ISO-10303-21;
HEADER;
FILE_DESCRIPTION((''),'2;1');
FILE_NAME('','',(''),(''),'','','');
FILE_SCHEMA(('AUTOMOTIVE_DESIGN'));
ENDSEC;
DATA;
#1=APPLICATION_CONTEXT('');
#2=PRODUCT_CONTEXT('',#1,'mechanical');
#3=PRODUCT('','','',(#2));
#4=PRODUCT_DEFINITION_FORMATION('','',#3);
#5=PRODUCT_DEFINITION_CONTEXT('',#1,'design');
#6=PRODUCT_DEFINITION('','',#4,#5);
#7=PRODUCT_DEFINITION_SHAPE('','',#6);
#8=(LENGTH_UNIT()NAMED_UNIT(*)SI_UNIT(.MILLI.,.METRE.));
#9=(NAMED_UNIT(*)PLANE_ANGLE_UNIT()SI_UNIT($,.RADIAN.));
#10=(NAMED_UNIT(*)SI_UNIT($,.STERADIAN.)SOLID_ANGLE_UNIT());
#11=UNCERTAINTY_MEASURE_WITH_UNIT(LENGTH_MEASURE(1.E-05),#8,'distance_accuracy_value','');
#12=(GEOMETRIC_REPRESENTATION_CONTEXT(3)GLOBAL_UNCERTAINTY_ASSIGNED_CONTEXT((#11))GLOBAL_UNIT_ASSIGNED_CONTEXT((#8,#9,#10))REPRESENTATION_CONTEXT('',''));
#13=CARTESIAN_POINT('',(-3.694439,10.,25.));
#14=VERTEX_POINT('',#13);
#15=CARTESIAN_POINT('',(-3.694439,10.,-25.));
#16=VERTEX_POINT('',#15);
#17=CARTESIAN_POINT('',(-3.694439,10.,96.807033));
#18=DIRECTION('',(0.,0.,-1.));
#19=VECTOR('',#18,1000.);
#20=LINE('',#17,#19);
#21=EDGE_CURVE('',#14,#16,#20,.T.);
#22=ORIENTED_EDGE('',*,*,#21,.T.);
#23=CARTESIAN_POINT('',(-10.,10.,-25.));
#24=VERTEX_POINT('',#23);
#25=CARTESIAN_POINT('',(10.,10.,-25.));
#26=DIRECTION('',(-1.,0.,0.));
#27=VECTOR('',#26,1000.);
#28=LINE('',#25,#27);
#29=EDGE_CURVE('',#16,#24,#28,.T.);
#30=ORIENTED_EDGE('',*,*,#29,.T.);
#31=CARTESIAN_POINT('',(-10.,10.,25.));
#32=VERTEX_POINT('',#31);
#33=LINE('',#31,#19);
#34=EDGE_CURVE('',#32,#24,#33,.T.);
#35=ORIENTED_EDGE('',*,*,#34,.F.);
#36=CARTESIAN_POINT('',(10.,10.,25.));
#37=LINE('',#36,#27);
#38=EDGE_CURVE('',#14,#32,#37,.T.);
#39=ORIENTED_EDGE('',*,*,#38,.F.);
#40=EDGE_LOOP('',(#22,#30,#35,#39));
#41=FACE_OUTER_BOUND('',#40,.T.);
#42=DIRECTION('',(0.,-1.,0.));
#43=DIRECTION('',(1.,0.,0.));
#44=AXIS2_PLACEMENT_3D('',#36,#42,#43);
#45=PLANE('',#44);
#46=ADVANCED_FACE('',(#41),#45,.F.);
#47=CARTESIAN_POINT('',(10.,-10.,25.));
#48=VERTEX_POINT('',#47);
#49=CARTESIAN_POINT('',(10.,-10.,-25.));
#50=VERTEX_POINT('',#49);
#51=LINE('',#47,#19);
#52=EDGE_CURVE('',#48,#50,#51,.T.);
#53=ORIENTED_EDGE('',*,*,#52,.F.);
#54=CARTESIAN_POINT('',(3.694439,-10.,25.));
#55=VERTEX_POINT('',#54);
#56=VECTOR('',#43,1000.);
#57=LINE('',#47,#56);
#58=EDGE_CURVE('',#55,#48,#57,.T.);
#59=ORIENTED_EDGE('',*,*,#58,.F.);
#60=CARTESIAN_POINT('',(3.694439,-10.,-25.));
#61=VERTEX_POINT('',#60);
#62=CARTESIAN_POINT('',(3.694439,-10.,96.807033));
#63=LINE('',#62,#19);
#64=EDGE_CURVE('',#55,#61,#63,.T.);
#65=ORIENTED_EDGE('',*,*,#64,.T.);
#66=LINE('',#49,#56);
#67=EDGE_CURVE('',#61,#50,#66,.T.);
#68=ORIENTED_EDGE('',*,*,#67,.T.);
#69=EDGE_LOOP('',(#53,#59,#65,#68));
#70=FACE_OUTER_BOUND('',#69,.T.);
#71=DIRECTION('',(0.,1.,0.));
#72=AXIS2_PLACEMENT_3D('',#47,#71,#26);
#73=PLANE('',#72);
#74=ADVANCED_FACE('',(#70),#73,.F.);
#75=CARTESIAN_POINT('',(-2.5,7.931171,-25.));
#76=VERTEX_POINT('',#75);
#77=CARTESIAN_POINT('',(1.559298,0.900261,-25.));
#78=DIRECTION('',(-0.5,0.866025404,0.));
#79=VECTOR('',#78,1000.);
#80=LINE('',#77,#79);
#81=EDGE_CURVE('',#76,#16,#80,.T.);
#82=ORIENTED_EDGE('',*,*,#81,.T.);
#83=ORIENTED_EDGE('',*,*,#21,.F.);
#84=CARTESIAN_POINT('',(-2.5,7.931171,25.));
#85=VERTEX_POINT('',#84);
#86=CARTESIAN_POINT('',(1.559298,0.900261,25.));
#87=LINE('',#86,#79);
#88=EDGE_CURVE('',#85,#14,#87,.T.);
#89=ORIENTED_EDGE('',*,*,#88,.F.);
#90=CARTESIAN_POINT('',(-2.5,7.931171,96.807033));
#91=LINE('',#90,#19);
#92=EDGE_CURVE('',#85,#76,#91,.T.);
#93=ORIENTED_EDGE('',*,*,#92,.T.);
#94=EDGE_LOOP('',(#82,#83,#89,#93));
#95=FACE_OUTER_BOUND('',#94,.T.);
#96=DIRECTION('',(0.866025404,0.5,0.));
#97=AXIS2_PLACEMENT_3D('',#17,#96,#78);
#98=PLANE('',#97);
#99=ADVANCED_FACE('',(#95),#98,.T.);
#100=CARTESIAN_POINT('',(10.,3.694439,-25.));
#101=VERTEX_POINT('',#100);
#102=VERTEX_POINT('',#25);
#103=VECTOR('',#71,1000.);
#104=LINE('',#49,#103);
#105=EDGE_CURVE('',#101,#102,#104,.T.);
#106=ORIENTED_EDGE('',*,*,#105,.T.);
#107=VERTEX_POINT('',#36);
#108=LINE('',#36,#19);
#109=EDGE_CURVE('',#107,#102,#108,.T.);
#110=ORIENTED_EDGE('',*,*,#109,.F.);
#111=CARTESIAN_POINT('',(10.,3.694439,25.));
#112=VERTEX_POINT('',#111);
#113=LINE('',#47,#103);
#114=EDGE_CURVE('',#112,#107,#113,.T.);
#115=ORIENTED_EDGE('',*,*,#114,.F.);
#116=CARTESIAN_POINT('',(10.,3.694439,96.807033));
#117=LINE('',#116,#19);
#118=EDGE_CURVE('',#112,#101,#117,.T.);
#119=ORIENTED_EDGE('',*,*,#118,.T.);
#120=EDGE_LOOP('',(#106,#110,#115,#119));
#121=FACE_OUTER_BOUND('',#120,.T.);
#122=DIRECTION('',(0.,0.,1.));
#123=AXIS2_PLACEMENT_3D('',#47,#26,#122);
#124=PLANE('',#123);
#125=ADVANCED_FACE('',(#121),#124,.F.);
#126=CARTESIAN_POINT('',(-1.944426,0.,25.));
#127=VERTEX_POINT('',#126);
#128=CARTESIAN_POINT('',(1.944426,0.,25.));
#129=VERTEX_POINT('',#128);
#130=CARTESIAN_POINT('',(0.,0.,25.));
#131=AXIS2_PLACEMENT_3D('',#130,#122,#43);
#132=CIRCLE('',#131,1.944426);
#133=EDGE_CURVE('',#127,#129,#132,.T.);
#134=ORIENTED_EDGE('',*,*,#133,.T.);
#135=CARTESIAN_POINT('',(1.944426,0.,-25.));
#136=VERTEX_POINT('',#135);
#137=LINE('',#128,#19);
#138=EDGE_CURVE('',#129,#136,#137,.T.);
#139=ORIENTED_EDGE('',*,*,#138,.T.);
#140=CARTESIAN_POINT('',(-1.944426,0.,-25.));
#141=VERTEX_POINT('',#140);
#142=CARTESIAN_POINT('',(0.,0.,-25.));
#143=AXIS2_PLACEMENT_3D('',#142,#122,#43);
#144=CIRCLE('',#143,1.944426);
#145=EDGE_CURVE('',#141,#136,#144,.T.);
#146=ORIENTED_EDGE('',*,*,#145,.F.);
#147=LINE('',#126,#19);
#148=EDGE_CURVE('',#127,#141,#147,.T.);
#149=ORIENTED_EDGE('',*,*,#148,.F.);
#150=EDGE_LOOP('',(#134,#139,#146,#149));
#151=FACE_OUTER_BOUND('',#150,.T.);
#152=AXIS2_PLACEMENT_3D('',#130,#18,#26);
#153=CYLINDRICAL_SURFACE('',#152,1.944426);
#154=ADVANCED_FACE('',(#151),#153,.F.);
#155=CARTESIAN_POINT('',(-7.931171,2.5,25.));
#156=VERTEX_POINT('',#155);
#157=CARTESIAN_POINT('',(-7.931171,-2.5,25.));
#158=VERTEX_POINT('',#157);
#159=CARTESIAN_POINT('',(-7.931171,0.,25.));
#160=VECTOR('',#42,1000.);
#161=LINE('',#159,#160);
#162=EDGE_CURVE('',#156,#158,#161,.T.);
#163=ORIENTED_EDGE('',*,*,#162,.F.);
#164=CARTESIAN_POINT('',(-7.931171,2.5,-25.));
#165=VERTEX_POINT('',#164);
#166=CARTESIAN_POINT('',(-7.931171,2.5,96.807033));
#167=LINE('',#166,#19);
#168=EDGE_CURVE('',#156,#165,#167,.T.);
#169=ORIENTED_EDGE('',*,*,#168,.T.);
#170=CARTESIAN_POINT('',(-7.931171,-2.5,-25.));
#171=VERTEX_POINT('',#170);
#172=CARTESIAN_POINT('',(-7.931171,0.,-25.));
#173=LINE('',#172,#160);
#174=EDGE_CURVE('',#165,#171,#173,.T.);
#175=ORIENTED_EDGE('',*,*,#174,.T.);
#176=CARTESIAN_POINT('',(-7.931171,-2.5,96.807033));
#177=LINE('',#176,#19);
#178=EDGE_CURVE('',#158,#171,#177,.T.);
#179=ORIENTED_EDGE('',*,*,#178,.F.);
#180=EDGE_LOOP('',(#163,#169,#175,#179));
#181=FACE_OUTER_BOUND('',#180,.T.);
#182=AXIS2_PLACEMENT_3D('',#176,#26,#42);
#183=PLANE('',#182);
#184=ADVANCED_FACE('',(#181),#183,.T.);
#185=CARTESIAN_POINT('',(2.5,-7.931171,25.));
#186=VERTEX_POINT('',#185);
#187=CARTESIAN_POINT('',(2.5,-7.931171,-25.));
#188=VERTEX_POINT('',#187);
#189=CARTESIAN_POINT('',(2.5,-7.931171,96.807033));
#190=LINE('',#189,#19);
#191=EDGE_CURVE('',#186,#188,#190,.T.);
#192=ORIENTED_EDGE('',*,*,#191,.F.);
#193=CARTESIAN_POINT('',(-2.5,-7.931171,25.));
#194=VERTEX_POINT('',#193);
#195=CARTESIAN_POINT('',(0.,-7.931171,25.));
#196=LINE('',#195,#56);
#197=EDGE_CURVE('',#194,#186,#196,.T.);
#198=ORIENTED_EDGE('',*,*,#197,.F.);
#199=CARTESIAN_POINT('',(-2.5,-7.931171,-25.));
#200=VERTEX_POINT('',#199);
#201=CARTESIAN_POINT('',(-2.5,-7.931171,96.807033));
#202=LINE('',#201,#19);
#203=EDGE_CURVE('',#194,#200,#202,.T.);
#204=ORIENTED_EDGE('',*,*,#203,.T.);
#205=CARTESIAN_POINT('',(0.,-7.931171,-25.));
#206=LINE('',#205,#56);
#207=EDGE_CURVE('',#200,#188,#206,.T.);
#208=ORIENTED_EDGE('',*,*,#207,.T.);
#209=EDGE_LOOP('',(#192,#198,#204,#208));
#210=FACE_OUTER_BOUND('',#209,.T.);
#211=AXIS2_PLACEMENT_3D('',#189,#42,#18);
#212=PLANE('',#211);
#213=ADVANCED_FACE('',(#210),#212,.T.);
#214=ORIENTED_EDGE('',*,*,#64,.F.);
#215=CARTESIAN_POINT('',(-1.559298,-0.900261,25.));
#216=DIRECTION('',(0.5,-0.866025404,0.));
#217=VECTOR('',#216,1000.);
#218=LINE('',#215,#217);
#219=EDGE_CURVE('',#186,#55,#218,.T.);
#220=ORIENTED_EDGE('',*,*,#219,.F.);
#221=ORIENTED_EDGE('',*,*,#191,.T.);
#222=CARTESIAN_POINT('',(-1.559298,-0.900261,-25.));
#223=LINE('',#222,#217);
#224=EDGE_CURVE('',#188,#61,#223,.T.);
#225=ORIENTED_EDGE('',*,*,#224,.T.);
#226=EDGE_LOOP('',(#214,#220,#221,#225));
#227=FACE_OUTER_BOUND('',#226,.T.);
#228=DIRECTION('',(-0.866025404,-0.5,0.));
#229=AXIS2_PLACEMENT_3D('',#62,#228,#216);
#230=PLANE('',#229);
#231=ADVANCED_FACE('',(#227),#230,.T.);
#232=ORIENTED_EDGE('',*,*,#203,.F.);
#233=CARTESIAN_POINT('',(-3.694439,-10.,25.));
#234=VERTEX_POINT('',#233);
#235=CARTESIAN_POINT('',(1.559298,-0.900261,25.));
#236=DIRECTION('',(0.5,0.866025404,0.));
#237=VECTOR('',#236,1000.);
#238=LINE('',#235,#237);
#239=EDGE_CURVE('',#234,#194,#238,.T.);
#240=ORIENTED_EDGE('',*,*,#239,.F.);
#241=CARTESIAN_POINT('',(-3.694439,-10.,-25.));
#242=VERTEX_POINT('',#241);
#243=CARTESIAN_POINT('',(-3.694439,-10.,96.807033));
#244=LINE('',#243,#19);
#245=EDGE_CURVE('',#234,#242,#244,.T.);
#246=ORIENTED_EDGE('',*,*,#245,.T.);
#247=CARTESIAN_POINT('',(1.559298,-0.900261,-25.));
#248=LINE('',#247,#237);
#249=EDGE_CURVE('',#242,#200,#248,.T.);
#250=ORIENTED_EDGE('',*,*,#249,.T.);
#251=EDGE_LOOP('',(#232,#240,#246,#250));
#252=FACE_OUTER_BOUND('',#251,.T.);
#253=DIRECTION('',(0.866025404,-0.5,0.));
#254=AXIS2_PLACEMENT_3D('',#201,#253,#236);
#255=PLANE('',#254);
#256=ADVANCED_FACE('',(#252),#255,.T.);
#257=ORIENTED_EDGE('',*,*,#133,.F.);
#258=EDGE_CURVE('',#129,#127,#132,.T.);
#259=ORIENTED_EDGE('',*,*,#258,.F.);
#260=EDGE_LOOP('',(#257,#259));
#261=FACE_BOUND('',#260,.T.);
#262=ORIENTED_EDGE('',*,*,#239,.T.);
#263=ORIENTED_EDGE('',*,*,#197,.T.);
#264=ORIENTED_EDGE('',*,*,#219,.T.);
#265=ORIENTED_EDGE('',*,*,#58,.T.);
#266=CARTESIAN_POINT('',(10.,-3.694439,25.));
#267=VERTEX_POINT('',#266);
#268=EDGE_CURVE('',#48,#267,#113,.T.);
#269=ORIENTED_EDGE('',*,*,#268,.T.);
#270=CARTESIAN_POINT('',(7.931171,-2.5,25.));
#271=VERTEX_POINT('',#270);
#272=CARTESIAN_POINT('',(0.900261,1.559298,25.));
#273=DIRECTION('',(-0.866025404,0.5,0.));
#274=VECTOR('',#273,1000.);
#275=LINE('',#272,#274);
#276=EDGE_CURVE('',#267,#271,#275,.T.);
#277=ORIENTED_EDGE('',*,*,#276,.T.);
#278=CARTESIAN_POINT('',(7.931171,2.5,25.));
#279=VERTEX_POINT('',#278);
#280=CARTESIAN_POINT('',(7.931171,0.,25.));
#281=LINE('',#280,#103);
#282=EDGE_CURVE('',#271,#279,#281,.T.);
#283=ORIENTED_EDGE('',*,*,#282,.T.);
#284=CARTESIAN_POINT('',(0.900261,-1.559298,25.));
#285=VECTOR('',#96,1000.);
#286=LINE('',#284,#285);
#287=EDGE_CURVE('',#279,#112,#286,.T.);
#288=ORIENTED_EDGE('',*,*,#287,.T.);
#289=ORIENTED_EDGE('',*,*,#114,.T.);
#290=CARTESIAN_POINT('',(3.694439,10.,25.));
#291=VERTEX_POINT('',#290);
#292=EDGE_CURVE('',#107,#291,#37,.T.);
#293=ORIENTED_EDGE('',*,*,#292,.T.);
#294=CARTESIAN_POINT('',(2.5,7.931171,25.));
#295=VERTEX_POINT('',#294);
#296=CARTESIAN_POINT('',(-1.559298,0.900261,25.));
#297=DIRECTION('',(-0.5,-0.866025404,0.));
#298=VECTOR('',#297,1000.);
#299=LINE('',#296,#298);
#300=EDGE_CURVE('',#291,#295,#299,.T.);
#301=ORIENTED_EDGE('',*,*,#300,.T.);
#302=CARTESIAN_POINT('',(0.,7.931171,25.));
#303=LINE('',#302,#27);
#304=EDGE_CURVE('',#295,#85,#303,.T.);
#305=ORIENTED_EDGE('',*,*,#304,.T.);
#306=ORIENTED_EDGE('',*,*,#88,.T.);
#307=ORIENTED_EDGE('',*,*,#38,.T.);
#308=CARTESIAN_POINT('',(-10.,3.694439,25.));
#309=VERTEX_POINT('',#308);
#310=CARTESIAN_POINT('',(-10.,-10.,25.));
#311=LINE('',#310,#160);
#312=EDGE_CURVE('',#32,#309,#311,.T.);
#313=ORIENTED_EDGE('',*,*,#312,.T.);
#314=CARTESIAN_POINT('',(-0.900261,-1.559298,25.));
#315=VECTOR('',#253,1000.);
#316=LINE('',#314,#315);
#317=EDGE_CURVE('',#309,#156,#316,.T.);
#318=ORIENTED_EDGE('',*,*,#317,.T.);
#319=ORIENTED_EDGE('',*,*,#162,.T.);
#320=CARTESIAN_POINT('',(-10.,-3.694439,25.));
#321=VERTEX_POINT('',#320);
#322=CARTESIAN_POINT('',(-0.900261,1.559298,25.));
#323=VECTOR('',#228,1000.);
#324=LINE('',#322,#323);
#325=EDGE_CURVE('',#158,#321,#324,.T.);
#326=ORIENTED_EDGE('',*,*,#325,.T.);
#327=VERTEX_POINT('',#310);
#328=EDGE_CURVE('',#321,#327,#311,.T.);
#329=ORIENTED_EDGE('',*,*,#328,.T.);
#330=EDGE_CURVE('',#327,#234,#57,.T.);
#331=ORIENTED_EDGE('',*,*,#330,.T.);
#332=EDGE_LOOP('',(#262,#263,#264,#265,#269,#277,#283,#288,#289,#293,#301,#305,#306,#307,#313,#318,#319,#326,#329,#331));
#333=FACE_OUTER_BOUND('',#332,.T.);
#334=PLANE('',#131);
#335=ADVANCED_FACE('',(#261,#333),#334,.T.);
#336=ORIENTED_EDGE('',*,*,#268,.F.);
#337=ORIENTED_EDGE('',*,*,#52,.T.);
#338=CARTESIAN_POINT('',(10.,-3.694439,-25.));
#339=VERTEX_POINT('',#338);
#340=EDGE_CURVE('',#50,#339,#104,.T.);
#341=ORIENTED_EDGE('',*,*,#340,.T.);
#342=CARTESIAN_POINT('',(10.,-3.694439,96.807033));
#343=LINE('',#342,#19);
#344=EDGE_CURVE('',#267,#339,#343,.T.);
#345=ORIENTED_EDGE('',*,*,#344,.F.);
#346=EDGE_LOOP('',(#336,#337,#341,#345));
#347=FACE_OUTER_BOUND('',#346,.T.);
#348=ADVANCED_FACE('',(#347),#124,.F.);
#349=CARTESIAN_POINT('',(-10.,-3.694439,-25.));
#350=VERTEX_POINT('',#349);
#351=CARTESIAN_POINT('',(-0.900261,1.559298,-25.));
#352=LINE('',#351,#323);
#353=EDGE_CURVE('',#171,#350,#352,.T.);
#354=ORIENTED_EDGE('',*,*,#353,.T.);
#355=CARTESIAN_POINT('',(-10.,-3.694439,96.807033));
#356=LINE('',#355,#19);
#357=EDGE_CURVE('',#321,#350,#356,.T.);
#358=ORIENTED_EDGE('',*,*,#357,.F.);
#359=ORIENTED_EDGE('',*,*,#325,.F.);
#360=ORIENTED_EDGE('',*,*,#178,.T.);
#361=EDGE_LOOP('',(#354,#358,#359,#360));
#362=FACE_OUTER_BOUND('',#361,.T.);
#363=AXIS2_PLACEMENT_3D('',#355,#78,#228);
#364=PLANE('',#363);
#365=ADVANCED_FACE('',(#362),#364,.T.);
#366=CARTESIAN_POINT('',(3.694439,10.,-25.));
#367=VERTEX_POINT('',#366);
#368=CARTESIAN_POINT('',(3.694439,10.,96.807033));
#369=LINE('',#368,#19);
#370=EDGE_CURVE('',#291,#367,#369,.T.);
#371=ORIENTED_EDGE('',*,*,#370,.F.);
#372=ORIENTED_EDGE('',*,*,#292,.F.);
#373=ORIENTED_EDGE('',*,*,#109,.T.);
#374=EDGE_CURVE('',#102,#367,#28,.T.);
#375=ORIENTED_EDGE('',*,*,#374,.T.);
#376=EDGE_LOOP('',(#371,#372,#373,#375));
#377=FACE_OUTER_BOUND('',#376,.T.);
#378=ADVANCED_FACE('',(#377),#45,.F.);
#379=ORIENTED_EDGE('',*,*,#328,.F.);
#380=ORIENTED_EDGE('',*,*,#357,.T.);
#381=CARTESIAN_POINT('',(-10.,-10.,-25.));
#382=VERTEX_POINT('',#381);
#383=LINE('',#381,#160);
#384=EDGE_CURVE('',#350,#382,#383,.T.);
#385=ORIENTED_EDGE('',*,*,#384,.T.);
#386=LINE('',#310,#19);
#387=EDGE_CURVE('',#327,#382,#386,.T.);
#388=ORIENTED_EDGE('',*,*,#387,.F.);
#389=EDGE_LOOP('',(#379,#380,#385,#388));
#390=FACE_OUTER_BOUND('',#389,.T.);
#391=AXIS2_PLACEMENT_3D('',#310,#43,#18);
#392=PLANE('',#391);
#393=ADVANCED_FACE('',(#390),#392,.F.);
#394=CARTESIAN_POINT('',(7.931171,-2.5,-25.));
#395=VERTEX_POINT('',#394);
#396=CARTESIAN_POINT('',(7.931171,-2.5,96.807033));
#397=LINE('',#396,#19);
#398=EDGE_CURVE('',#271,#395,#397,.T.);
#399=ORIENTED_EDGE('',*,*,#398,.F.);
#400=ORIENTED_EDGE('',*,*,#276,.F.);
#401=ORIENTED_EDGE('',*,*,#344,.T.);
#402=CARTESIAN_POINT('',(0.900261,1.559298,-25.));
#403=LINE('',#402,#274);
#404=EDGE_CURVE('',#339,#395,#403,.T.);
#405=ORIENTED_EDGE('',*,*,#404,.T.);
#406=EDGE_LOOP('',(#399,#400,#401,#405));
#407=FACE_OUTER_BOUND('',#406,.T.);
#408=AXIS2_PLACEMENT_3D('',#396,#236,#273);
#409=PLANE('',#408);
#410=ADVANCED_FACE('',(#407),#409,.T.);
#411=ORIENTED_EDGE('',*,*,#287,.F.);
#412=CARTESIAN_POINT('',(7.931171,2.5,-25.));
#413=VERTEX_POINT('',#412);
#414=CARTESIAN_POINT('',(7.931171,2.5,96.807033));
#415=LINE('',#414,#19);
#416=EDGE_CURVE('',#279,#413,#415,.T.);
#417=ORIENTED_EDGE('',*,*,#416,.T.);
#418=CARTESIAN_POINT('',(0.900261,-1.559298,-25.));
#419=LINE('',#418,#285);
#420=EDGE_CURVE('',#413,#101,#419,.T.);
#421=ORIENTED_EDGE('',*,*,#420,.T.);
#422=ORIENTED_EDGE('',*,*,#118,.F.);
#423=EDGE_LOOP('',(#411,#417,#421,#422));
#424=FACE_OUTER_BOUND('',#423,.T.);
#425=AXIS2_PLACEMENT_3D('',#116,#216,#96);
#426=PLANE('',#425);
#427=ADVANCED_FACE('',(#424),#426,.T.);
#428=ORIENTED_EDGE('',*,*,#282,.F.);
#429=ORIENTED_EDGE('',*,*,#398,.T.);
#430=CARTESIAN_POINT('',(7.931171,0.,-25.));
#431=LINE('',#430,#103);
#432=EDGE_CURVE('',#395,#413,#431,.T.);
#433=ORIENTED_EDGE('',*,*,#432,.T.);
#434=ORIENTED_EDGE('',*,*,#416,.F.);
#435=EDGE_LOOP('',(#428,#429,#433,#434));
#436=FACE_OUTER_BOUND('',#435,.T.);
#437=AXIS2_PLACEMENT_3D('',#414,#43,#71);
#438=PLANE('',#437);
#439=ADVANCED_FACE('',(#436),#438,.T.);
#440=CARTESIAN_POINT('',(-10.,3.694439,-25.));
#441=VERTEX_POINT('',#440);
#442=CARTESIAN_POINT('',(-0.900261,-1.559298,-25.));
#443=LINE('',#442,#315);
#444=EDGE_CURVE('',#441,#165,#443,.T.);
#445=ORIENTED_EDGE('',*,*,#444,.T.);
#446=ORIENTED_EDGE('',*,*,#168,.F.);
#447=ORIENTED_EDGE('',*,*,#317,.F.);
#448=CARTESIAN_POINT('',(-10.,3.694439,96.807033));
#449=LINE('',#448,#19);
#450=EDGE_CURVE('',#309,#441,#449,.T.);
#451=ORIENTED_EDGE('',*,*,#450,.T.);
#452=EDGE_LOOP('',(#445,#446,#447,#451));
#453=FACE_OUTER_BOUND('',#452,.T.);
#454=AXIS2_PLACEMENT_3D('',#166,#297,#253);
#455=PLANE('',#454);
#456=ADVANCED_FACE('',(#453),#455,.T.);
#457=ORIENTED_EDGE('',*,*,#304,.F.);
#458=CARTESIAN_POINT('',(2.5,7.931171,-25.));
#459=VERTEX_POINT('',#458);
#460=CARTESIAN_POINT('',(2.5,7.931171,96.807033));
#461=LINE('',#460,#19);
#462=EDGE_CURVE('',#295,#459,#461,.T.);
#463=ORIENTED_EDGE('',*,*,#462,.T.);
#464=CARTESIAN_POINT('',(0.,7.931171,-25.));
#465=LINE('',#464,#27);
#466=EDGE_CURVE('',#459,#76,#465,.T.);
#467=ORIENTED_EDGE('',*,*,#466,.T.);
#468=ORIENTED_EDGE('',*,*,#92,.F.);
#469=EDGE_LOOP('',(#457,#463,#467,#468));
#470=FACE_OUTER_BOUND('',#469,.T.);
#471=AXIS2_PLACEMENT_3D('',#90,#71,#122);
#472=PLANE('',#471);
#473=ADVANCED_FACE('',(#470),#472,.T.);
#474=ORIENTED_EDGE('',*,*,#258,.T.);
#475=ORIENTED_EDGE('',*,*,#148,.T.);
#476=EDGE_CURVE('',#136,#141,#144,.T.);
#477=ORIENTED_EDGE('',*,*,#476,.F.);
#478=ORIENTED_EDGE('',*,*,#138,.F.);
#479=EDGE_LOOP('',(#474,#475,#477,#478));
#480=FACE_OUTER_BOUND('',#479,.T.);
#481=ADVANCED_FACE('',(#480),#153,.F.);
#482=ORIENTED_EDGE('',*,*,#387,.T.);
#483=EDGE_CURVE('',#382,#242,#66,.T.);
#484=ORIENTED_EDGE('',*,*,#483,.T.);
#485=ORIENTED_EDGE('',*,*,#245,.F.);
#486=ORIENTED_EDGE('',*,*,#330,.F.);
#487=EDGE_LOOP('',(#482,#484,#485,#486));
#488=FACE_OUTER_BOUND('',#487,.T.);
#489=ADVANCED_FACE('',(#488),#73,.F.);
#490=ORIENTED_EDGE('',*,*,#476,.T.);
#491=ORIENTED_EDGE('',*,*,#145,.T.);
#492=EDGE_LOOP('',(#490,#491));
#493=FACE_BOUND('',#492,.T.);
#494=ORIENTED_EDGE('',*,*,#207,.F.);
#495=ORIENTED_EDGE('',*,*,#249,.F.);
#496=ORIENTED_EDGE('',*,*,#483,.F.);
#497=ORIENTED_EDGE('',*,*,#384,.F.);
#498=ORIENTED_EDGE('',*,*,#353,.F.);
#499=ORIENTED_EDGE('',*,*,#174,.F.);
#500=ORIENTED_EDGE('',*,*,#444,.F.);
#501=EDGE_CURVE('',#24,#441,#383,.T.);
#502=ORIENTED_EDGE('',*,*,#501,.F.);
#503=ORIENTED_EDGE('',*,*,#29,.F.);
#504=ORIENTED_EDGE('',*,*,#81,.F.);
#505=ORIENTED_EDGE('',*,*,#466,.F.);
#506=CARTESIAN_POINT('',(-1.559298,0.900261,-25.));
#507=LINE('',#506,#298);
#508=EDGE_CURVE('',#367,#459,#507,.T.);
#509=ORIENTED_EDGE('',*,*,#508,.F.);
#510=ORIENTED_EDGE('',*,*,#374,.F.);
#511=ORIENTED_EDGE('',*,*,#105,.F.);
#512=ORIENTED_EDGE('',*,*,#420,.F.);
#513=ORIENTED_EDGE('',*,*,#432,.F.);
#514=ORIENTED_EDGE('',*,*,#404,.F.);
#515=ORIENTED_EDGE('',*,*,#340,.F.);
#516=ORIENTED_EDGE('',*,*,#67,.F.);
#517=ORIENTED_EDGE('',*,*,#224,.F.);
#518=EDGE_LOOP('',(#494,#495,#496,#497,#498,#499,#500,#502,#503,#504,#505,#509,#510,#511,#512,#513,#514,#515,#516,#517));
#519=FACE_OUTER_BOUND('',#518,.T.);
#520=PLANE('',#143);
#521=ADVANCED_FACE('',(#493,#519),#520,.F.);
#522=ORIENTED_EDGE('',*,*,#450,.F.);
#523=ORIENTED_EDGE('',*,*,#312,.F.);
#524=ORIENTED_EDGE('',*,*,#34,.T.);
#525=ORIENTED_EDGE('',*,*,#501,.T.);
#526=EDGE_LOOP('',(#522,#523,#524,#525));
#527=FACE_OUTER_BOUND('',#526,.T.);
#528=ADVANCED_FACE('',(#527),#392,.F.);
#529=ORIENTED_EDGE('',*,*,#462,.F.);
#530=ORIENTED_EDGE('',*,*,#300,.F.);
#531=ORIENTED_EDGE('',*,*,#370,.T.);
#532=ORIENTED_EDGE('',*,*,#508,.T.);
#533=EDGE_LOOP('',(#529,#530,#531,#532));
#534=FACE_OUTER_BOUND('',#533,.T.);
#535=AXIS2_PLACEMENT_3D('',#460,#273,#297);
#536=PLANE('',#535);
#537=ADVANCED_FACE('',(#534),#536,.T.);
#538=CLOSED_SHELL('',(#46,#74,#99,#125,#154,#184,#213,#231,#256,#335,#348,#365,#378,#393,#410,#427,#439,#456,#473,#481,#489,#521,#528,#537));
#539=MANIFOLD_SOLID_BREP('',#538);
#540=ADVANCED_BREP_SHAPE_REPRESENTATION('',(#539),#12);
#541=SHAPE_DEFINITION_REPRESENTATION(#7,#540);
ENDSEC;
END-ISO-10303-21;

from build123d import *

# Parameters (mm, degrees)
SKETCH_1_W               = 20
SKETCH_1_H               = 20
SKETCH_1_R               = 1.94442565
EXTRUDE_1_DEPTH          = 25
CUT_EXTRUDE_1_DEPTH      = 52.961524227
PATTERN_CIRCULAR_1_COUNT = 4


with BuildPart() as part:
    # 草图1 → 凸台-拉伸1 (new, symmetric)
    with BuildSketch(Plane.XY):
        Rectangle(SKETCH_1_W, SKETCH_1_H)
        Circle(SKETCH_1_R, mode=Mode.SUBTRACT)
    extrude(amount=EXTRUDE_1_DEPTH, both=True)

    # 草图2 → 切除-拉伸1 (cut, symmetric)
    with BuildSketch(Plane.XY.offset(25)):
        Polygon((-32.933615203, 60.643738676), (-3.694439046, 10), (-2.5, 7.931170886), (2.5, 7.931170886), (3.694439046, 10), (32.933615203, 60.643738676), (32.933615203, 177.600443305), (-32.933615203, 177.600443305), align=None)
    cut_extrude_1 = extrude(amount=CUT_EXTRUDE_1_DEPTH, both=True, mode=Mode.SUBTRACT)

    # 阵列(圆周)1: 切除-拉伸1 ×4 about axis
    pattern_circular_1_axis = Axis((0, 0, 25), (0, 0, -1))
    for i in range(1, PATTERN_CIRCULAR_1_COUNT):
        add(cut_extrude_1.rotate(pattern_circular_1_axis, i * 360 / PATTERN_CIRCULAR_1_COUNT), mode=Mode.SUBTRACT)


solid = part.part
